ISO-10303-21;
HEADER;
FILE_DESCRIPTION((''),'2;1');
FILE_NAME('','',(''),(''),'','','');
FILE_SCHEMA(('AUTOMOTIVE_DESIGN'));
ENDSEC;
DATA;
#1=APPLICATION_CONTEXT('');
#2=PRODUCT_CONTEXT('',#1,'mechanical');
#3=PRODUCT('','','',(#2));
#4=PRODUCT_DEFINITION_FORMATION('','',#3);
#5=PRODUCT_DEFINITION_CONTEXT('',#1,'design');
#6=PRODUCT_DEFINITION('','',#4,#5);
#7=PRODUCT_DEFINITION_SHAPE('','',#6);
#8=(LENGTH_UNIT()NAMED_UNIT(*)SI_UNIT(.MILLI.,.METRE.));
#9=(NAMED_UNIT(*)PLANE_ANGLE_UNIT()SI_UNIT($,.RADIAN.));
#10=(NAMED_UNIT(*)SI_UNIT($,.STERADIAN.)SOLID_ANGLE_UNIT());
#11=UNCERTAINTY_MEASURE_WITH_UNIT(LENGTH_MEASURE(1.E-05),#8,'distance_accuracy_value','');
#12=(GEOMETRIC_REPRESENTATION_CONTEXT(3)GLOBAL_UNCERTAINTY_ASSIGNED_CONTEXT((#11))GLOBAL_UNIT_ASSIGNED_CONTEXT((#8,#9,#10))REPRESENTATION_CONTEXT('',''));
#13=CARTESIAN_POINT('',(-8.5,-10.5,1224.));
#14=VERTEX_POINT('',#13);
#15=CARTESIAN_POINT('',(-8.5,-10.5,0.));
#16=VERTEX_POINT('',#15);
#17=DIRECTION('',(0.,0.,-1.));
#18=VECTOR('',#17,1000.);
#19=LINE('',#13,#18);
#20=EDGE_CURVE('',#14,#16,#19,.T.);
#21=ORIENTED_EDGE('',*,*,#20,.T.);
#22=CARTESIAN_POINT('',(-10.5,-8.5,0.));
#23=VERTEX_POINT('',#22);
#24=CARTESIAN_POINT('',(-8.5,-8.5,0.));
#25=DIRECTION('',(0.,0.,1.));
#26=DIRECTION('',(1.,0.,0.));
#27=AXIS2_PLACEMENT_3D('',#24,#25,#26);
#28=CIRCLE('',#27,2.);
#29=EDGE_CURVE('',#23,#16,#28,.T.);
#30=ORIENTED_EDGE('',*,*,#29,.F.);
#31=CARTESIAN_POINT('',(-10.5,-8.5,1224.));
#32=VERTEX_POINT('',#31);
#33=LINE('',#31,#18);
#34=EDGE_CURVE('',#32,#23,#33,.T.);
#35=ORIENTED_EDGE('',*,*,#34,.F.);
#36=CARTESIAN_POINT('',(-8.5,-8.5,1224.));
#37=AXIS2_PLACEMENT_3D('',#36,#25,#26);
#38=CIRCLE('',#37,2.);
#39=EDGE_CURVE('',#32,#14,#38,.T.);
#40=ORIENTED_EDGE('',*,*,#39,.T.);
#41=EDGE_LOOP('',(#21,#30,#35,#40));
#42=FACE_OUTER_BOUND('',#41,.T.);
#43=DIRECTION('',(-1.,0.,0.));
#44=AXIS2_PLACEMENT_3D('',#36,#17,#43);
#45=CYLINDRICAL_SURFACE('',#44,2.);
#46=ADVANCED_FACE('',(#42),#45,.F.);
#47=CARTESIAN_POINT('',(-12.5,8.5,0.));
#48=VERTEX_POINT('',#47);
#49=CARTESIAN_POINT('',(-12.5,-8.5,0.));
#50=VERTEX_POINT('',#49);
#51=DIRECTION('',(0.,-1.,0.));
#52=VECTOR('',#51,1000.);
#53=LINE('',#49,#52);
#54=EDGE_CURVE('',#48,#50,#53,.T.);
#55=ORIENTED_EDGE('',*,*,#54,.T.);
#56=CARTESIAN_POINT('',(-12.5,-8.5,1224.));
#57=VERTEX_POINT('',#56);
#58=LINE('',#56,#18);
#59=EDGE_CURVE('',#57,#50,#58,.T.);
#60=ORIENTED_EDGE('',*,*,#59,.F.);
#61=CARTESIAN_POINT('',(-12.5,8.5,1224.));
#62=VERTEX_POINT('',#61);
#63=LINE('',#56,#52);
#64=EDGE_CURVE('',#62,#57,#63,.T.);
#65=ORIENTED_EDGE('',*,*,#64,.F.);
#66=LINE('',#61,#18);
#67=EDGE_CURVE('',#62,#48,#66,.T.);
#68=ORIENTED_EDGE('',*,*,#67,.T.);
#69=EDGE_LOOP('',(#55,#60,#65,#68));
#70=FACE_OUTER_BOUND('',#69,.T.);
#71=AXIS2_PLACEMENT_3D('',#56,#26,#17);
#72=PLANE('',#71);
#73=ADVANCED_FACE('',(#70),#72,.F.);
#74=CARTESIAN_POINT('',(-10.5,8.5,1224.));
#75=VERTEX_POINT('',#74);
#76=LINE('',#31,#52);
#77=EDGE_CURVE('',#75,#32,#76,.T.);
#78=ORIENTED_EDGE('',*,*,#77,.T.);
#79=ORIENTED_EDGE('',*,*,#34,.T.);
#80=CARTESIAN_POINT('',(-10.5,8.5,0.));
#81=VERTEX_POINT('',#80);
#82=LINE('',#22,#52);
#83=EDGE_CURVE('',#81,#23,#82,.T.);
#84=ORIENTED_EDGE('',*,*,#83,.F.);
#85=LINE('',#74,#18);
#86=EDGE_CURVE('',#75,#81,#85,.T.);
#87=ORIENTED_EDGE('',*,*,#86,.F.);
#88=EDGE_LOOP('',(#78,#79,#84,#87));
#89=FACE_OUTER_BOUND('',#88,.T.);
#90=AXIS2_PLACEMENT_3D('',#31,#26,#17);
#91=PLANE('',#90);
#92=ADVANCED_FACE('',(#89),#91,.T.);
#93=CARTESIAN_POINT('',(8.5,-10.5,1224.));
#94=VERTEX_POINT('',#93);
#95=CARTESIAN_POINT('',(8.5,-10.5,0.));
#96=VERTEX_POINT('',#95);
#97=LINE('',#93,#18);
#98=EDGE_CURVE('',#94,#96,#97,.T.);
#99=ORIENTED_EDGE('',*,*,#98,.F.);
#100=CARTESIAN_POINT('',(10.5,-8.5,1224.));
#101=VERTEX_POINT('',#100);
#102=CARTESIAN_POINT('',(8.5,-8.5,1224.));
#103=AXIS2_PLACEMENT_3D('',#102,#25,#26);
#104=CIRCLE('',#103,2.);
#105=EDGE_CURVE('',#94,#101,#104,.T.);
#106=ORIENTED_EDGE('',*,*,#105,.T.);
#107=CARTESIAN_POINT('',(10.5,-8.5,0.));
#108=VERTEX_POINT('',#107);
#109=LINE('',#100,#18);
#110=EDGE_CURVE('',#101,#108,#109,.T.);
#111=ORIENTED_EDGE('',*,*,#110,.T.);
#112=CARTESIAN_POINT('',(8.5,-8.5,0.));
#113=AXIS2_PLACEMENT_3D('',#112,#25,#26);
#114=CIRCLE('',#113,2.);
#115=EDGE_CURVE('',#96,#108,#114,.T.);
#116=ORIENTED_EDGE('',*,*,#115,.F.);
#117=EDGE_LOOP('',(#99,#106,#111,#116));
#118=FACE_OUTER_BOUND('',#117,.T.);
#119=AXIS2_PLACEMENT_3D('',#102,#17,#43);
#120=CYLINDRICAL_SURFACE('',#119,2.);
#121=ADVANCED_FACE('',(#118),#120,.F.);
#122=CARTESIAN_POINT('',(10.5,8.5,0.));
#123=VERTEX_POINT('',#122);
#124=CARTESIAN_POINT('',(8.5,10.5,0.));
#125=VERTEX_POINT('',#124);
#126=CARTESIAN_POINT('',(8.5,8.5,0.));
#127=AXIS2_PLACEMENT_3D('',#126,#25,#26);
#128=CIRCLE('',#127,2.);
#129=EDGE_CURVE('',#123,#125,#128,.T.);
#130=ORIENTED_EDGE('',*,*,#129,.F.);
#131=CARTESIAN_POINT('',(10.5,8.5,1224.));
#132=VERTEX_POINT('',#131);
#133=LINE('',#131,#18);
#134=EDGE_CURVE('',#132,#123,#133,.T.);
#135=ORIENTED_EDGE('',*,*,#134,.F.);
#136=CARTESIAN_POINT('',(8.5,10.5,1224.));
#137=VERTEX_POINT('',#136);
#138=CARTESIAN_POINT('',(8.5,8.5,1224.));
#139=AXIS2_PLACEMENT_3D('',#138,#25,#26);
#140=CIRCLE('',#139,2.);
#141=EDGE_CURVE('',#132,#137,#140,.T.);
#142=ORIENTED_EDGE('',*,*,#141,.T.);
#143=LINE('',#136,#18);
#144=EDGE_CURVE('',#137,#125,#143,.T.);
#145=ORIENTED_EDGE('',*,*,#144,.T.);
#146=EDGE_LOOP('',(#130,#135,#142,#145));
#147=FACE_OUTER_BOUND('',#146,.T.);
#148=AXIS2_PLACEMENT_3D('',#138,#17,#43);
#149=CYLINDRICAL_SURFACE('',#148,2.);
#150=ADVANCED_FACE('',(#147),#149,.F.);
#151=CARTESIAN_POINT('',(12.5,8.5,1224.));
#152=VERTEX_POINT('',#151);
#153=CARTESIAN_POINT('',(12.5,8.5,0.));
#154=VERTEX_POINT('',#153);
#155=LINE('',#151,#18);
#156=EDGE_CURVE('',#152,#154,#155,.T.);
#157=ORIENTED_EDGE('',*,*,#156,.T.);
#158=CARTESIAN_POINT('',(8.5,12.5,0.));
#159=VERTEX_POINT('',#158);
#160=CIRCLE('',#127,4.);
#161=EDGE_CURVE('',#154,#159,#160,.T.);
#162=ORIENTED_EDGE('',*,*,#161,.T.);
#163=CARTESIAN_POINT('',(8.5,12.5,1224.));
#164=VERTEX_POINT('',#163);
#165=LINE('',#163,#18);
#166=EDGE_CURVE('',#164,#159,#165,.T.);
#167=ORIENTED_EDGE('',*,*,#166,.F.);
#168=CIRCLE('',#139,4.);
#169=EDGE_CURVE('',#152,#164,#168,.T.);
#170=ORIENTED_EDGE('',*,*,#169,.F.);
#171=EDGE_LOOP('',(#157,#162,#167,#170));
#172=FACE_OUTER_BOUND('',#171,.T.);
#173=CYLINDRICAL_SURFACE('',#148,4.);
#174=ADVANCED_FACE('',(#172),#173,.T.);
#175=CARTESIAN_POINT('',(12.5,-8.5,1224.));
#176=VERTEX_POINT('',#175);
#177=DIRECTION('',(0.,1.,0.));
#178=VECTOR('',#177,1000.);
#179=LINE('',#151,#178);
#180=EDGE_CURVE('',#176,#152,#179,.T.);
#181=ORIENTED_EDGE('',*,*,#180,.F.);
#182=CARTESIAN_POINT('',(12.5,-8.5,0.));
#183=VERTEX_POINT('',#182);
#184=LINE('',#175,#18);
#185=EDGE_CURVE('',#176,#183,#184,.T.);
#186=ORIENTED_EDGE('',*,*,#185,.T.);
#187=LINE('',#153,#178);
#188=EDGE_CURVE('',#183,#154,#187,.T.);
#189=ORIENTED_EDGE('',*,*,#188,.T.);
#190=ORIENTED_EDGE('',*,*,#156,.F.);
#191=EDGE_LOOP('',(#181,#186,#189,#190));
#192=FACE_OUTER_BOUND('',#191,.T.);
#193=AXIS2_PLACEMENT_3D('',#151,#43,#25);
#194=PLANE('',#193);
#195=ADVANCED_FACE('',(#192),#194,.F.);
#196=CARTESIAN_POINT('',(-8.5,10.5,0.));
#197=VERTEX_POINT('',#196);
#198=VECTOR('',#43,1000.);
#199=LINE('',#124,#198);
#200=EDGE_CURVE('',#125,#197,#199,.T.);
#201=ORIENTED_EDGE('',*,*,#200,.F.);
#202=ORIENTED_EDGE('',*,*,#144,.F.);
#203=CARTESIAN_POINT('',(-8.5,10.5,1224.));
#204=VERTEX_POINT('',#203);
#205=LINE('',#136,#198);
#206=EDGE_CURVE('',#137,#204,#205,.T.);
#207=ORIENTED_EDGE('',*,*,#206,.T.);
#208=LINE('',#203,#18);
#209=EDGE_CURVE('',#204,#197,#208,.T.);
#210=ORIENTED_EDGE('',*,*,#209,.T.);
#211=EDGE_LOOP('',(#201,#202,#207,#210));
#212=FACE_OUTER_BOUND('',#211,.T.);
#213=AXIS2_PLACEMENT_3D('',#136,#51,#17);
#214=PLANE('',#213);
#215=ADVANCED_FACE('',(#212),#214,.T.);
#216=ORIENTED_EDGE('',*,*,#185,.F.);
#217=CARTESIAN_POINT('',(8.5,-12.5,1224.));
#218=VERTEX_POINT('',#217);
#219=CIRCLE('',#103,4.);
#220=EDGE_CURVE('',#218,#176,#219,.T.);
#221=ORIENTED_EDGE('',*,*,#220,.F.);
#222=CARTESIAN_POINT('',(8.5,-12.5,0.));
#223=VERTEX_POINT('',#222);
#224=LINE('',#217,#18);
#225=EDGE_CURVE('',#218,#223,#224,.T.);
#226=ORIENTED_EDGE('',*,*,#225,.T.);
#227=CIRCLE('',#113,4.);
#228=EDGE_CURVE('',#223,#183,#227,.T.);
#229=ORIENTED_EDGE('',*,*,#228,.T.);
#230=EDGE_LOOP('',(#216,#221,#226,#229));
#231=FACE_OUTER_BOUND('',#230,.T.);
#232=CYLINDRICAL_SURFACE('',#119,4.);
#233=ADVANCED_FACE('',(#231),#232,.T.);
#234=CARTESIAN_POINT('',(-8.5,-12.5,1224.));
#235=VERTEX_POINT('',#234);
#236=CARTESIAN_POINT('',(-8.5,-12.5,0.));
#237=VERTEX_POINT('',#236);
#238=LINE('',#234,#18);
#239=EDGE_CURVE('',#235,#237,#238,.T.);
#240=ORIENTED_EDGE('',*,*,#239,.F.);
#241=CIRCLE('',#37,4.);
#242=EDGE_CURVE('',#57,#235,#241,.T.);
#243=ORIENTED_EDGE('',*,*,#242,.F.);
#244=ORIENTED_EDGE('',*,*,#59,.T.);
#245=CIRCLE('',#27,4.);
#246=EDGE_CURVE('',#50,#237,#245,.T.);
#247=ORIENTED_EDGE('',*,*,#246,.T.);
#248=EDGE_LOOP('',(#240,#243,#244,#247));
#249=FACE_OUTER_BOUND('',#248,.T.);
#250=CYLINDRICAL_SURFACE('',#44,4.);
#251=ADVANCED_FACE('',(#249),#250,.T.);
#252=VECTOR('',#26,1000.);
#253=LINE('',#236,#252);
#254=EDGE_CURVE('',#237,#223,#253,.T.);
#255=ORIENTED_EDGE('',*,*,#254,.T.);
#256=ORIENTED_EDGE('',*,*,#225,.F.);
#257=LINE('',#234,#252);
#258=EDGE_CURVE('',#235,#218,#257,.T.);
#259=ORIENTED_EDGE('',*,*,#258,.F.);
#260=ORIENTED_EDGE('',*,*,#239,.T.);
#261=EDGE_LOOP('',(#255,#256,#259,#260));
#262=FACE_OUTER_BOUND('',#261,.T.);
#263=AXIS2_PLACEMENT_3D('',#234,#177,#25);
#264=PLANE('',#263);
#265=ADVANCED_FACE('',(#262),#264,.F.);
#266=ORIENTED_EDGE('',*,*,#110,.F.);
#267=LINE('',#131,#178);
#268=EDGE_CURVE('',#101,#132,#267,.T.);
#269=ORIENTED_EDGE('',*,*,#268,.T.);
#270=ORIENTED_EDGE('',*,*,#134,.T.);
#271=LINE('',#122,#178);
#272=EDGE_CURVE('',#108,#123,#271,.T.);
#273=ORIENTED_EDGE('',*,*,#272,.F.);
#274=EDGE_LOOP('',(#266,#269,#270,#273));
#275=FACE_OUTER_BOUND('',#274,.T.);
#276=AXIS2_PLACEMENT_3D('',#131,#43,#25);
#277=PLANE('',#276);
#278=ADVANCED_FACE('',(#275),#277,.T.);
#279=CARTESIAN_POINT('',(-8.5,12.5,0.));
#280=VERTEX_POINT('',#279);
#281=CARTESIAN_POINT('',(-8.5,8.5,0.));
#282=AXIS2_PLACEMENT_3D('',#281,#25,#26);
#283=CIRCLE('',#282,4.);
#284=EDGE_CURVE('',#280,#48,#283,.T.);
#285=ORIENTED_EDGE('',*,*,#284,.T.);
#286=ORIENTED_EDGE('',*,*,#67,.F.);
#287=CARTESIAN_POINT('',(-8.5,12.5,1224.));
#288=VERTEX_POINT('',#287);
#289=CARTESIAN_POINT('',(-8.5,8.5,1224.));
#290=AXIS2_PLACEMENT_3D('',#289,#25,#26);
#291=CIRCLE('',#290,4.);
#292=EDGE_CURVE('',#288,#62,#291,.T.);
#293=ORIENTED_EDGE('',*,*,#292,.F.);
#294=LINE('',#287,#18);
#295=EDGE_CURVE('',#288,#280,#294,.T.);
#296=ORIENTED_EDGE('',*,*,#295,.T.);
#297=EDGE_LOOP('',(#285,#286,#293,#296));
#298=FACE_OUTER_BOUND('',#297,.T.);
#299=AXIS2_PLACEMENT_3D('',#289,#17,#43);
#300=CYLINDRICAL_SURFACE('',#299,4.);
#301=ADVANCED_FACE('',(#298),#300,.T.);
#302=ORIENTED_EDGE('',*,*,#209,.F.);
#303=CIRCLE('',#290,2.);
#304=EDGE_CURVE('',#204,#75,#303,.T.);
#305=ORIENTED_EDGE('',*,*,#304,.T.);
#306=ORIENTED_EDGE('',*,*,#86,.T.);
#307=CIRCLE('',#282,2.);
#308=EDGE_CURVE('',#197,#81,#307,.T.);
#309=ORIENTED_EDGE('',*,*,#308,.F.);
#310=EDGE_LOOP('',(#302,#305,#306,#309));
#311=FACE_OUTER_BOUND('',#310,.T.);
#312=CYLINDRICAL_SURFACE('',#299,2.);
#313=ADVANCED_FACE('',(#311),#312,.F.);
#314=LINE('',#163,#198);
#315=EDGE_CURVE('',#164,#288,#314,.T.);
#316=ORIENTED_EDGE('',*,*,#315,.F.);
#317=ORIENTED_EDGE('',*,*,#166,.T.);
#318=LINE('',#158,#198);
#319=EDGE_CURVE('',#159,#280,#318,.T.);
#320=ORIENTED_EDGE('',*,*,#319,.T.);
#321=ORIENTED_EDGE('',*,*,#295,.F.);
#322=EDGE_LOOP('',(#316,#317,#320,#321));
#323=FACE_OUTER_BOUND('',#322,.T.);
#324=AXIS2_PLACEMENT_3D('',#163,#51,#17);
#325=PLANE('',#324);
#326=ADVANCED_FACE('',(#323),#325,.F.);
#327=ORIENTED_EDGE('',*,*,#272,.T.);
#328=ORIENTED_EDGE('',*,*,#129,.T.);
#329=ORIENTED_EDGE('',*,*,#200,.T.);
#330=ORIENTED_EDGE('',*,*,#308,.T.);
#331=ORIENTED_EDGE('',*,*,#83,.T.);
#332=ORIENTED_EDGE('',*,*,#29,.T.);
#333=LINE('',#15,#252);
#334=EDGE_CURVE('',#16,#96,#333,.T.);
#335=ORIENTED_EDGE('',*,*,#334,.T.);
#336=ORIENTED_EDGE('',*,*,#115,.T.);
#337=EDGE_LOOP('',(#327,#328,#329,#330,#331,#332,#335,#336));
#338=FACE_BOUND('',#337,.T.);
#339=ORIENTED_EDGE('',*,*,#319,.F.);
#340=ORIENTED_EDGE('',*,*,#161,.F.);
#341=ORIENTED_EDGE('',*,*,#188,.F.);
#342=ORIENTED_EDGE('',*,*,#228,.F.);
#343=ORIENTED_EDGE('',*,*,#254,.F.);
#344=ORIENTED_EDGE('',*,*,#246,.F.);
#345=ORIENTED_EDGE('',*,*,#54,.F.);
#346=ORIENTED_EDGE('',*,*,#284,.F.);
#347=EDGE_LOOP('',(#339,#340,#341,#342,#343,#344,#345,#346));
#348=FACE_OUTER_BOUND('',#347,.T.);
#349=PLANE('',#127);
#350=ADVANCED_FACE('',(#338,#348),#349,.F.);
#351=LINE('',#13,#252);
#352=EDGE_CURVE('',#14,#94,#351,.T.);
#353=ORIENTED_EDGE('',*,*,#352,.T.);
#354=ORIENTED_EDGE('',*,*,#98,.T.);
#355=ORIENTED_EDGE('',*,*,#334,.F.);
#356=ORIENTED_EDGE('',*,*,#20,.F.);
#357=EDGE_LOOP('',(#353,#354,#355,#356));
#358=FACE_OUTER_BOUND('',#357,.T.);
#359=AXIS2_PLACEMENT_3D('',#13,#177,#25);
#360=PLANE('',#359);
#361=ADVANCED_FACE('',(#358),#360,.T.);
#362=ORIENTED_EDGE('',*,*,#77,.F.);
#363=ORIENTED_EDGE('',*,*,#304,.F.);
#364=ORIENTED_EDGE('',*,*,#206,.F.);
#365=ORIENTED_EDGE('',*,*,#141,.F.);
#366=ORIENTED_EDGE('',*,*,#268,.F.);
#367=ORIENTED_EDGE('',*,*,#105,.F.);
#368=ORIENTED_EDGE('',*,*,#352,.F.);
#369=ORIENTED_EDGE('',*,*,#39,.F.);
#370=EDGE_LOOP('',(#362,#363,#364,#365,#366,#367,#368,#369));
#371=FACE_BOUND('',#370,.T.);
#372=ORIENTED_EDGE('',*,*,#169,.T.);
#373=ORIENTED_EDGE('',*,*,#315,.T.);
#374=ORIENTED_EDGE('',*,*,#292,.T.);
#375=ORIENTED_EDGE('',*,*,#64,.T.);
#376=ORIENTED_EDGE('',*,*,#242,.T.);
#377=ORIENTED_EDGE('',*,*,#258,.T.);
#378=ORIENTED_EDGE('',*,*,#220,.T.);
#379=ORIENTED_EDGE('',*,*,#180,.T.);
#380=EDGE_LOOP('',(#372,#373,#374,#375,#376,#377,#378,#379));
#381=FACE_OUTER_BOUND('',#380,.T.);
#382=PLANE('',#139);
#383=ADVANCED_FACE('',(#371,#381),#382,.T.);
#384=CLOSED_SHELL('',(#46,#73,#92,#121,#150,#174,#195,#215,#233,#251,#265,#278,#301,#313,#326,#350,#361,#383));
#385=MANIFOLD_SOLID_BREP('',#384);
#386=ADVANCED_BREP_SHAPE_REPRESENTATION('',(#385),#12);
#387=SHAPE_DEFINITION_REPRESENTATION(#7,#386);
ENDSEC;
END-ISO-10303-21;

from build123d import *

# Parameters (mm, degrees)
BOSS_EXTRUDE1_DEPTH = 1224


with BuildPart() as part:
    # Sketch1 → Boss-Extrude1 (new body)
    with BuildSketch(Plane.XY):
        with BuildLine():
            Line((-8.5, -12.5), (8.5, -12.5))
            ThreePointArc((8.5, -12.5), (11.328427125, -11.328427125), (12.5, -8.5))
            Line((12.5, -8.5), (12.5, 8.5))
            ThreePointArc((12.5, 8.5), (11.328427125, 11.328427125), (8.5, 12.5))
            Line((8.5, 12.5), (-8.5, 12.5))
            ThreePointArc((-8.5, 12.5), (-11.328427125, 11.328427125), (-12.5, 8.5))
            Line((-12.5, 8.5), (-12.5, -8.5))
            ThreePointArc((-12.5, -8.5), (-11.328427125, -11.328427125), (-8.5, -12.5))
        make_face()
        with BuildLine():
            Line((-8.5, -10.5), (8.5, -10.5))
            ThreePointArc((8.5, -10.5), (9.914213562, -9.914213562), (10.5, -8.5))
            Line((10.5, -8.5), (10.5, 8.5))
            ThreePointArc((10.5, 8.5), (9.914213562, 9.914213562), (8.5, 10.5))
            Line((8.5, 10.5), (-8.5, 10.5))
            ThreePointArc((-8.5, 10.5), (-9.914213562, 9.914213562), (-10.5, 8.5))
            Line((-10.5, 8.5), (-10.5, -8.5))
            ThreePointArc((-10.5, -8.5), (-9.914213562, -9.914213562), (-8.5, -10.5))
        make_face(mode=Mode.SUBTRACT)
    extrude(amount=BOSS_EXTRUDE1_DEPTH)


solid = part.part
